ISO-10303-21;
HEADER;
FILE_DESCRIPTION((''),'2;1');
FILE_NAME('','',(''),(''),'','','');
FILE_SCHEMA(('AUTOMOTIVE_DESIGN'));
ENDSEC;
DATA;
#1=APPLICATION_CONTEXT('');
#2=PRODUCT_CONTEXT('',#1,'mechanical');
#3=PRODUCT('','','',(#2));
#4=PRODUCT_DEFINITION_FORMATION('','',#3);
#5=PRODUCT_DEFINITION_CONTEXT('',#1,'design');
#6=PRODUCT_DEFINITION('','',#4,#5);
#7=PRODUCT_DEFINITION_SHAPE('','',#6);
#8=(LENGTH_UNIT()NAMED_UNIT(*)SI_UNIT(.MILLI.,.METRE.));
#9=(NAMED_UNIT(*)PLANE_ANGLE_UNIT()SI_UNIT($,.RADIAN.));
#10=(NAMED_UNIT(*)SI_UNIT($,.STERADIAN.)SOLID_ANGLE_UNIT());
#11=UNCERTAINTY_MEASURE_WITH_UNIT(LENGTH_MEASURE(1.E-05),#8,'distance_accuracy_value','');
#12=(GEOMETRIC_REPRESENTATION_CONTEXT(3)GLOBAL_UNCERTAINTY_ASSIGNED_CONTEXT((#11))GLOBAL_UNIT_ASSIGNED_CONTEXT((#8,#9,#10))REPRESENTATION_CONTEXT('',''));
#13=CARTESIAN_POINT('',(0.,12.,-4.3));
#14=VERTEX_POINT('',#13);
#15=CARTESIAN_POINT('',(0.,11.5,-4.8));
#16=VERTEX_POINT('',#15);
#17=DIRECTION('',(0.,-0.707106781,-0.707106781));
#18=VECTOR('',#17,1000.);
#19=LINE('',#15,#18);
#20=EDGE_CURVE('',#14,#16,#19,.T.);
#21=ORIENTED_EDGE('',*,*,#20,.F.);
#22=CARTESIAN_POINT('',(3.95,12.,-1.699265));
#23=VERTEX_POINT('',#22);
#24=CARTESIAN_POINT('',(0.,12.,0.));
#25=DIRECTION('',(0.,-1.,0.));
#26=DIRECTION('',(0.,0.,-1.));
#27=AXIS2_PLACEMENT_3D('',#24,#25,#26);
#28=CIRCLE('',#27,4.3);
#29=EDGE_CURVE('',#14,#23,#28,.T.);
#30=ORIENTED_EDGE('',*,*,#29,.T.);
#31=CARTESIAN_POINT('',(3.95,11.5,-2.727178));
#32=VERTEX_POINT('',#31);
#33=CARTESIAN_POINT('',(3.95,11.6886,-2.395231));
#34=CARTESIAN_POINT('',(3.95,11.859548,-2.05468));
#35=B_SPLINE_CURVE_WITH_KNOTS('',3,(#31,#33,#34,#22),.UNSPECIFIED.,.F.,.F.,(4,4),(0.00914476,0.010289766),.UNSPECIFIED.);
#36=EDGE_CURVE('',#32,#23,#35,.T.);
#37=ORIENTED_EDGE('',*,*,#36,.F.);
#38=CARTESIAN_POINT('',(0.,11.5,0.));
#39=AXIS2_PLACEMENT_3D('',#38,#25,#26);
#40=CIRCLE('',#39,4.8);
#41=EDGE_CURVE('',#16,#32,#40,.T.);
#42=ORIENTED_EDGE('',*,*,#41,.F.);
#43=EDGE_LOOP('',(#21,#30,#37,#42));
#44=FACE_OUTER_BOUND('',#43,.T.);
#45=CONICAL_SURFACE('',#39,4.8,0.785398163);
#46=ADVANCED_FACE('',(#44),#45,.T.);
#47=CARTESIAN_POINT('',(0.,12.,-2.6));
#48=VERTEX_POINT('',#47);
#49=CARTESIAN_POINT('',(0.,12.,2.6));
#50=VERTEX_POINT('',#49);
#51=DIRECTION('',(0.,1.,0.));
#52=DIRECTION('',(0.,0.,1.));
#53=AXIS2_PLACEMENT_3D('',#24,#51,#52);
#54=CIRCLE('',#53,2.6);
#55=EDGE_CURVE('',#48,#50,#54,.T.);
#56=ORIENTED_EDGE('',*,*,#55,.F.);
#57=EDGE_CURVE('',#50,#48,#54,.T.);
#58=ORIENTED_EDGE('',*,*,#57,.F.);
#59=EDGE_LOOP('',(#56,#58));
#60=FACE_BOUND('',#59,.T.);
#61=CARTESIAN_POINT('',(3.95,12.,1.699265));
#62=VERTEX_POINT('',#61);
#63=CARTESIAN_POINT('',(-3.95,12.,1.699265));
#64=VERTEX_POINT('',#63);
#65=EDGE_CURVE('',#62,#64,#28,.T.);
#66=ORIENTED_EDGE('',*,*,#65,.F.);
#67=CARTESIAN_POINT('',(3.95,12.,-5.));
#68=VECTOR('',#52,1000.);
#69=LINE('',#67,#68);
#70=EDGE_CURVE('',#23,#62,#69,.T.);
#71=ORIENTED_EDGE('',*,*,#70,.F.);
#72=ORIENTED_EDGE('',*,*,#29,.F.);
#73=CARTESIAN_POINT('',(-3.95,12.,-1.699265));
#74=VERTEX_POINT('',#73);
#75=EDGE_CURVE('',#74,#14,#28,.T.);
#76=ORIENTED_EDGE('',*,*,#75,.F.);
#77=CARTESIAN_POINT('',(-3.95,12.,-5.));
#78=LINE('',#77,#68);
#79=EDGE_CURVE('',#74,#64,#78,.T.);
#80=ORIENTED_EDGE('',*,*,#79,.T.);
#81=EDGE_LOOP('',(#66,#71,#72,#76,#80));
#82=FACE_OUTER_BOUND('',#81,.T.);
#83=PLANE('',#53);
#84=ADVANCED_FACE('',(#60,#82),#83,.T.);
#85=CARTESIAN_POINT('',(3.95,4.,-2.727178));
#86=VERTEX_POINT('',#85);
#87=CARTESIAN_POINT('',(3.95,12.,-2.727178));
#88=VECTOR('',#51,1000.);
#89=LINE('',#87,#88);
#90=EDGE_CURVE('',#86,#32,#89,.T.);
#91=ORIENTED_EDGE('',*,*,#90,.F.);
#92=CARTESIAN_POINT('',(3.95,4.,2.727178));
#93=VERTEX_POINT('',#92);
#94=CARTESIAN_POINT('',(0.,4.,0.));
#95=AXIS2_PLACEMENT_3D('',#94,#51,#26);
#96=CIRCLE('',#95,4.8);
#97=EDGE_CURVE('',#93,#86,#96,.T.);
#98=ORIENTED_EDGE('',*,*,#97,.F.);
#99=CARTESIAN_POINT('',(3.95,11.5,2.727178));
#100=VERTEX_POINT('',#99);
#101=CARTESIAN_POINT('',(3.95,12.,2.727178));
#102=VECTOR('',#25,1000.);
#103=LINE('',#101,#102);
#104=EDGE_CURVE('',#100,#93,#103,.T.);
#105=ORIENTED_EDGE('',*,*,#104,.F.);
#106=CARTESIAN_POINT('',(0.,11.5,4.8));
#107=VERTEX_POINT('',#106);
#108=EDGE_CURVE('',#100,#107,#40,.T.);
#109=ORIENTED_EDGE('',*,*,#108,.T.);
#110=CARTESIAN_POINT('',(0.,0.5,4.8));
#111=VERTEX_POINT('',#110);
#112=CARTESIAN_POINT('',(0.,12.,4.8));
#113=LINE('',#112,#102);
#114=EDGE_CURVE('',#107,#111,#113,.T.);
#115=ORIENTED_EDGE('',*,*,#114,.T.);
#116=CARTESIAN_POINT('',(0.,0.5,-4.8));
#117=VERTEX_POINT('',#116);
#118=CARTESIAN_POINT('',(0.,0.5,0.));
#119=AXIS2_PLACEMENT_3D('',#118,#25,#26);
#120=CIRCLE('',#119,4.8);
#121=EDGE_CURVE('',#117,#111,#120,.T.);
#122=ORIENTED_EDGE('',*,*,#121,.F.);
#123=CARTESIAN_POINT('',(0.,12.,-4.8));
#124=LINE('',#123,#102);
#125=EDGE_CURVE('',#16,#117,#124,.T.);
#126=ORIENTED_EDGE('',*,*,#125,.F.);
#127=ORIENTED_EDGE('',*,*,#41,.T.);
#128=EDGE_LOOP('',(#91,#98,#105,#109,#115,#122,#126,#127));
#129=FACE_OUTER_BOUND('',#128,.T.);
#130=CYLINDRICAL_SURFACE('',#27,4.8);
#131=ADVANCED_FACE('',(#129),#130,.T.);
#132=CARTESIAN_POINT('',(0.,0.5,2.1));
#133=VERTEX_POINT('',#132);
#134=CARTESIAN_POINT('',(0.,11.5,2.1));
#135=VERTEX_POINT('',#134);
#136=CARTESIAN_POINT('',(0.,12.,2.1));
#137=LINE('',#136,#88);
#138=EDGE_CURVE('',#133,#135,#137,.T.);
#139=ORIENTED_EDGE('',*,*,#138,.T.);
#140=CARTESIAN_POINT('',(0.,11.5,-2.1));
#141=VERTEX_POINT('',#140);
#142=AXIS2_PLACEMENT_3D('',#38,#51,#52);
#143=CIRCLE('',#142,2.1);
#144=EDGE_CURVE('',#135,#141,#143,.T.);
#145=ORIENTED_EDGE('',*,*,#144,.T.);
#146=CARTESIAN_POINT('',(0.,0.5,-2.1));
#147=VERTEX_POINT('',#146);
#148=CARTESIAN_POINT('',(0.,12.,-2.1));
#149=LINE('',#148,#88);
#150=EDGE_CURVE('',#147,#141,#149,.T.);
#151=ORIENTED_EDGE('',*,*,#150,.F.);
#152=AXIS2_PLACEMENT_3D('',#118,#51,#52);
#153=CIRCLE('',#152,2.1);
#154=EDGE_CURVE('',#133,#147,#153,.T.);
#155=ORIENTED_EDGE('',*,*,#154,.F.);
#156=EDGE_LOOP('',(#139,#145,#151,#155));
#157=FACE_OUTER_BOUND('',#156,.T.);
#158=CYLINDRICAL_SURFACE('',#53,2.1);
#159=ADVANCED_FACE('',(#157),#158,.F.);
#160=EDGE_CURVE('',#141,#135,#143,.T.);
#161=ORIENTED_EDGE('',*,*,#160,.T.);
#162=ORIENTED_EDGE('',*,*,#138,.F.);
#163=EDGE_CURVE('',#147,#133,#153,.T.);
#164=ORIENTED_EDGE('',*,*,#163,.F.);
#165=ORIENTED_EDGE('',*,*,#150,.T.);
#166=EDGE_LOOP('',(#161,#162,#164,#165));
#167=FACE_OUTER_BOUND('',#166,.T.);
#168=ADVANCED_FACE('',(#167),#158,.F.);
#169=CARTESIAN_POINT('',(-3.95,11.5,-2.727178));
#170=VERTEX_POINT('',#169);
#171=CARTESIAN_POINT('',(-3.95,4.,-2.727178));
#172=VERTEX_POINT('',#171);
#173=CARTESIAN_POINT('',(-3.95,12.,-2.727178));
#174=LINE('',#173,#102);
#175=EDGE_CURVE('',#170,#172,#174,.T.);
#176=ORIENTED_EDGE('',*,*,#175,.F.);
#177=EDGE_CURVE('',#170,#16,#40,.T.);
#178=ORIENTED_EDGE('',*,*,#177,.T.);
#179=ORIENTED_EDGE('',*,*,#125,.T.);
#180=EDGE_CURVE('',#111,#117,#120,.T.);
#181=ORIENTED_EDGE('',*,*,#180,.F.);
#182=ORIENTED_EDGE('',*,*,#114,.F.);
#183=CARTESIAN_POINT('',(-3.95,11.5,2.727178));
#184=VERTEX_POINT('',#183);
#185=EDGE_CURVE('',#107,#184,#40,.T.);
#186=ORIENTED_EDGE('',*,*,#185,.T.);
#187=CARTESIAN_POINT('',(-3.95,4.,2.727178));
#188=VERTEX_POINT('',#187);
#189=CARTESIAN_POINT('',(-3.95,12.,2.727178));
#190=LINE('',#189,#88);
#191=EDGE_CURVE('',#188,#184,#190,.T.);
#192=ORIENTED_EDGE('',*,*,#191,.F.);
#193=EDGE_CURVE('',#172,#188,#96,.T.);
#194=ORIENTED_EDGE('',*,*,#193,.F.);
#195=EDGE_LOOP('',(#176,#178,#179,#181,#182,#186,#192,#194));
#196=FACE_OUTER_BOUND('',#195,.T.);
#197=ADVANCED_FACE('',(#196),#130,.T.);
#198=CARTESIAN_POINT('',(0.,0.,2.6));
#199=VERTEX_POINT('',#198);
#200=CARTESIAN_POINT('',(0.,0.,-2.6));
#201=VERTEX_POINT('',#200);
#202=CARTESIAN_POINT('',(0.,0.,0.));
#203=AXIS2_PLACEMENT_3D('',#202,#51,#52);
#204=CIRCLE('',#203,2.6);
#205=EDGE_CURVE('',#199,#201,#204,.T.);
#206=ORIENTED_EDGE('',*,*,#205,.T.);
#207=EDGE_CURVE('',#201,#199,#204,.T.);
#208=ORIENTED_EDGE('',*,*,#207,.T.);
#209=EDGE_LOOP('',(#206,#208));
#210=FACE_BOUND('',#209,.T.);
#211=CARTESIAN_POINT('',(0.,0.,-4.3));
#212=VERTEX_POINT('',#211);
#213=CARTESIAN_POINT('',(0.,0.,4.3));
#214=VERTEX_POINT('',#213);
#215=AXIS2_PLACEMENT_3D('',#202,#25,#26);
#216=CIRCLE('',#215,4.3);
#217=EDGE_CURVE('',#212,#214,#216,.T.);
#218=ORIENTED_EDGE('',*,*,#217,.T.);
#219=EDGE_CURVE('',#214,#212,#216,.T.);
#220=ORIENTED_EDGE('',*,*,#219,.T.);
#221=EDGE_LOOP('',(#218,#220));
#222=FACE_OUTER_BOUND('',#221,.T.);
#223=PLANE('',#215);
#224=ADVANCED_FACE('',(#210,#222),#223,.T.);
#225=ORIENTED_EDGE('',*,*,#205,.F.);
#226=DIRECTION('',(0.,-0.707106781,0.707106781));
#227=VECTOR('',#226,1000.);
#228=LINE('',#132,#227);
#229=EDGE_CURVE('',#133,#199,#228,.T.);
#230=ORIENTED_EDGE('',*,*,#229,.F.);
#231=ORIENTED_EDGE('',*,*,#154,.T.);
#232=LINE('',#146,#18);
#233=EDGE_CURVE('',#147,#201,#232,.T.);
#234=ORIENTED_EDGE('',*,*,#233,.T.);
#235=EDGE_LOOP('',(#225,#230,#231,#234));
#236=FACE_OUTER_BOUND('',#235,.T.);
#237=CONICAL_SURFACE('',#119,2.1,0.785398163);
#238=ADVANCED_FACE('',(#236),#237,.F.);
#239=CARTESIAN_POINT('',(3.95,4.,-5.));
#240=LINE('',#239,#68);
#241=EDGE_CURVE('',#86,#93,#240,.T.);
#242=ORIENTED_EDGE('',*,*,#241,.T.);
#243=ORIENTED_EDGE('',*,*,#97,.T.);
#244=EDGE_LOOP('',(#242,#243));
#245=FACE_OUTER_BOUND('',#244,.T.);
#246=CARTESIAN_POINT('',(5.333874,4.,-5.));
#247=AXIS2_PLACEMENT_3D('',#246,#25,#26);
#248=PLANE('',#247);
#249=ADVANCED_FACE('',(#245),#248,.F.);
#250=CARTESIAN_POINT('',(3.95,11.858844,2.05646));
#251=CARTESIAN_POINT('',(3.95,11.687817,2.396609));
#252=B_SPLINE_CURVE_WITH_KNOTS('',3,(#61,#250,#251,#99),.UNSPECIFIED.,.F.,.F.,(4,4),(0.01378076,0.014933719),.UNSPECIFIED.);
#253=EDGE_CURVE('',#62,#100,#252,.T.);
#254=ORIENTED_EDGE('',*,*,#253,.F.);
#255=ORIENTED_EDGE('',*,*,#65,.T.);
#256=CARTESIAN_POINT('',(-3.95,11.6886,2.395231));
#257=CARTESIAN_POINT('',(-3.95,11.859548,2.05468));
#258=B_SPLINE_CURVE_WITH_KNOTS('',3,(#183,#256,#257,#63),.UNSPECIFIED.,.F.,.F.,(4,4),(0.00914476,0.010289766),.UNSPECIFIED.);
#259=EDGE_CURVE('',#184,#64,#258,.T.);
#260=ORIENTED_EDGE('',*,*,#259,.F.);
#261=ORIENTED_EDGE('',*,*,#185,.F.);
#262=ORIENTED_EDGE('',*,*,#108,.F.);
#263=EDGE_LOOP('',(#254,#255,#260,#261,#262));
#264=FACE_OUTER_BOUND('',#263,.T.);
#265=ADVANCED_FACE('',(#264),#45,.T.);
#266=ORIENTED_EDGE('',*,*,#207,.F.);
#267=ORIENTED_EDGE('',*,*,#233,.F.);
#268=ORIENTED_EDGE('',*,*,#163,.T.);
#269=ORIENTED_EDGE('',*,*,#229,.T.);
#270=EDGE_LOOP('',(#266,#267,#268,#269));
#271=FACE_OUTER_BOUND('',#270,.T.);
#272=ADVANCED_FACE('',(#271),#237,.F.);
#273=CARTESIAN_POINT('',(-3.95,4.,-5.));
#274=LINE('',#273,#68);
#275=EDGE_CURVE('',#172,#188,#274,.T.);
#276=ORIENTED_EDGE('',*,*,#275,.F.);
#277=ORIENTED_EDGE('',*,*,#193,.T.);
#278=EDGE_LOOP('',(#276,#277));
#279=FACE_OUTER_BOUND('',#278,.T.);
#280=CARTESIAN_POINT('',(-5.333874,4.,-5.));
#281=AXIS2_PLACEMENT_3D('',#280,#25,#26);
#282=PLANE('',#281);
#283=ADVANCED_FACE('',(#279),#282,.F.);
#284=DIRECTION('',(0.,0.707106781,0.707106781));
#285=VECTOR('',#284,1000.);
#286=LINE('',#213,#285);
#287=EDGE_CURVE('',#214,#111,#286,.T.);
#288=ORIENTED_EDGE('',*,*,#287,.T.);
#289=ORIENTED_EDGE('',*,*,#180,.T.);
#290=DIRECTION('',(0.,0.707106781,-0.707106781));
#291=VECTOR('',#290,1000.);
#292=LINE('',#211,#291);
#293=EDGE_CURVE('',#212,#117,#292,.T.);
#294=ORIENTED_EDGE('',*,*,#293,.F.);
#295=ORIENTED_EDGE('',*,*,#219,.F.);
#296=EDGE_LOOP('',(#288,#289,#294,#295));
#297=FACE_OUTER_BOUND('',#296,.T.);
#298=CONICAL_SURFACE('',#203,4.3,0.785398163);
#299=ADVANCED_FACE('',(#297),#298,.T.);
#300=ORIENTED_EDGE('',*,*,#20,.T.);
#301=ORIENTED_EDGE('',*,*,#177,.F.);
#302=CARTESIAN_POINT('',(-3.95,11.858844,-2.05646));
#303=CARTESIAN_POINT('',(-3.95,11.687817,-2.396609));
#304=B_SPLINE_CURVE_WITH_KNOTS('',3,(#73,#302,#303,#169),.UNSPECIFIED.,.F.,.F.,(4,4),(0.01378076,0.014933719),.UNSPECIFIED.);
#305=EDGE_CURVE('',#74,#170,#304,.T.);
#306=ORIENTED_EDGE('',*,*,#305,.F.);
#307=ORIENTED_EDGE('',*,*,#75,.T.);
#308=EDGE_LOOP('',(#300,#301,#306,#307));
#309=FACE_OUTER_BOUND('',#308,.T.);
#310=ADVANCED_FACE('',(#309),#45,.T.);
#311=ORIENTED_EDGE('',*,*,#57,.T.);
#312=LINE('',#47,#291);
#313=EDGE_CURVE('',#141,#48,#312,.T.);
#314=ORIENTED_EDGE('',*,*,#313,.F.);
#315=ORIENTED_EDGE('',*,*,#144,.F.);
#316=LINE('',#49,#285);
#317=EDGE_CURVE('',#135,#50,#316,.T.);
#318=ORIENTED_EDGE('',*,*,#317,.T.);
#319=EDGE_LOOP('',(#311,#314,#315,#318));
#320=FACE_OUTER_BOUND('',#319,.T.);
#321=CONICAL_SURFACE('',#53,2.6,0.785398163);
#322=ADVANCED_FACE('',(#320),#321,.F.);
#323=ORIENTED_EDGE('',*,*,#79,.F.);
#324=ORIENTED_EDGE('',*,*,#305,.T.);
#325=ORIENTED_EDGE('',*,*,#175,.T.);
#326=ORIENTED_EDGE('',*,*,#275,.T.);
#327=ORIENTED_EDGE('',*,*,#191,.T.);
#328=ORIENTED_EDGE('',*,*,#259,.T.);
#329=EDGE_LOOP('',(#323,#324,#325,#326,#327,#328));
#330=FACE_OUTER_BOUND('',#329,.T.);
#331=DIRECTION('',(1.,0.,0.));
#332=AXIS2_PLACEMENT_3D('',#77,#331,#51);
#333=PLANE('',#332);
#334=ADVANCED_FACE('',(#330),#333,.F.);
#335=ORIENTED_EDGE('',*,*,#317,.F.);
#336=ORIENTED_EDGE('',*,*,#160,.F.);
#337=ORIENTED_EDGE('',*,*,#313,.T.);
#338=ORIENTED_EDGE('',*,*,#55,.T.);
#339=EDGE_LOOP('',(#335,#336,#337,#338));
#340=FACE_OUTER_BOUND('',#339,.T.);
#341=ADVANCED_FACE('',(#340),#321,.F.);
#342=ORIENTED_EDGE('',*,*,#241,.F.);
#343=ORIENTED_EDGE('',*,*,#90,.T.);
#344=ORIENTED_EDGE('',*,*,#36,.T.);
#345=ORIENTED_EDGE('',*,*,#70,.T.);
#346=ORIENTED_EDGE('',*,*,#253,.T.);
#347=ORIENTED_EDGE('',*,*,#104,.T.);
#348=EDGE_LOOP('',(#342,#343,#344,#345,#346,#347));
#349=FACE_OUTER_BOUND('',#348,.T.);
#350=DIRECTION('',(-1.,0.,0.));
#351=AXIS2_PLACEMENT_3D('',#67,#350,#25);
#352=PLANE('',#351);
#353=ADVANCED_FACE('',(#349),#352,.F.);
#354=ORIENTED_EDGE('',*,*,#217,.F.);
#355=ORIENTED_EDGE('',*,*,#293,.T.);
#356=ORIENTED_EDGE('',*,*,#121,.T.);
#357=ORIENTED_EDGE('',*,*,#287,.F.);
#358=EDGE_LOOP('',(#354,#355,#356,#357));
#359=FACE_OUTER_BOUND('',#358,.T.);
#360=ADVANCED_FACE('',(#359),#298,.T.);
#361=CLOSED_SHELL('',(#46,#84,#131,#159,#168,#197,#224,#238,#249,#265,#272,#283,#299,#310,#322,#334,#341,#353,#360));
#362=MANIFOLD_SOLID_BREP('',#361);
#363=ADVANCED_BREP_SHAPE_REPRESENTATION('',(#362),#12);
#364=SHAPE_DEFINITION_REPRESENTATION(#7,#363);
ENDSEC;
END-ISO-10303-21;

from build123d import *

# Parameters (mm, degrees)
SKETCH4_W          = 1.383873909
SKETCH4_H          = 8
CUT_EXTRUDE1_DEPTH = 5


with BuildPart() as part:
    # Sketch1 → Revolve1 (revolve)
    with BuildSketch(Plane.XY, mode=Mode.PRIVATE) as revolve1_sk:
        Polygon((0, 0), (4.3, 0), (4.8, 0.5), (4.8, 11.5), (4.3, 12), (0, 12), align=None)
    revolve(revolve1_sk.sketch.rotate(Axis((0, 12, 0), (0, 1, 0)), 90), axis=Axis((0, 12, 0), (0, 1, 0)))

    # Sketch3 → M5 Tapped Hole1 (revolve, cut)
    with BuildSketch(Plane(origin=(0, 12, 0), x_dir=(0, 0, 1), z_dir=(1, 0, 0))):
        Polygon((0, 0), (0, 12), (2.6, 12), (2.1, 11.5), (2.1, 0.5), (2.6, 0), align=None)
    revolve(axis=Axis((0, 18.35, 0), (0, -1, 0)), mode=Mode.SUBTRACT)

    # Sketch4 → Cut-Extrude1 (cut, symmetric)
    with BuildSketch(Plane.XY):
        with Locations((-4.641936955, 8)):
            Rectangle(SKETCH4_W, SKETCH4_H)
        with Locations((4.641936955, 8)):
            Rectangle(SKETCH4_W, SKETCH4_H)
    extrude(amount=CUT_EXTRUDE1_DEPTH, both=True, mode=Mode.SUBTRACT)


solid = part.part
